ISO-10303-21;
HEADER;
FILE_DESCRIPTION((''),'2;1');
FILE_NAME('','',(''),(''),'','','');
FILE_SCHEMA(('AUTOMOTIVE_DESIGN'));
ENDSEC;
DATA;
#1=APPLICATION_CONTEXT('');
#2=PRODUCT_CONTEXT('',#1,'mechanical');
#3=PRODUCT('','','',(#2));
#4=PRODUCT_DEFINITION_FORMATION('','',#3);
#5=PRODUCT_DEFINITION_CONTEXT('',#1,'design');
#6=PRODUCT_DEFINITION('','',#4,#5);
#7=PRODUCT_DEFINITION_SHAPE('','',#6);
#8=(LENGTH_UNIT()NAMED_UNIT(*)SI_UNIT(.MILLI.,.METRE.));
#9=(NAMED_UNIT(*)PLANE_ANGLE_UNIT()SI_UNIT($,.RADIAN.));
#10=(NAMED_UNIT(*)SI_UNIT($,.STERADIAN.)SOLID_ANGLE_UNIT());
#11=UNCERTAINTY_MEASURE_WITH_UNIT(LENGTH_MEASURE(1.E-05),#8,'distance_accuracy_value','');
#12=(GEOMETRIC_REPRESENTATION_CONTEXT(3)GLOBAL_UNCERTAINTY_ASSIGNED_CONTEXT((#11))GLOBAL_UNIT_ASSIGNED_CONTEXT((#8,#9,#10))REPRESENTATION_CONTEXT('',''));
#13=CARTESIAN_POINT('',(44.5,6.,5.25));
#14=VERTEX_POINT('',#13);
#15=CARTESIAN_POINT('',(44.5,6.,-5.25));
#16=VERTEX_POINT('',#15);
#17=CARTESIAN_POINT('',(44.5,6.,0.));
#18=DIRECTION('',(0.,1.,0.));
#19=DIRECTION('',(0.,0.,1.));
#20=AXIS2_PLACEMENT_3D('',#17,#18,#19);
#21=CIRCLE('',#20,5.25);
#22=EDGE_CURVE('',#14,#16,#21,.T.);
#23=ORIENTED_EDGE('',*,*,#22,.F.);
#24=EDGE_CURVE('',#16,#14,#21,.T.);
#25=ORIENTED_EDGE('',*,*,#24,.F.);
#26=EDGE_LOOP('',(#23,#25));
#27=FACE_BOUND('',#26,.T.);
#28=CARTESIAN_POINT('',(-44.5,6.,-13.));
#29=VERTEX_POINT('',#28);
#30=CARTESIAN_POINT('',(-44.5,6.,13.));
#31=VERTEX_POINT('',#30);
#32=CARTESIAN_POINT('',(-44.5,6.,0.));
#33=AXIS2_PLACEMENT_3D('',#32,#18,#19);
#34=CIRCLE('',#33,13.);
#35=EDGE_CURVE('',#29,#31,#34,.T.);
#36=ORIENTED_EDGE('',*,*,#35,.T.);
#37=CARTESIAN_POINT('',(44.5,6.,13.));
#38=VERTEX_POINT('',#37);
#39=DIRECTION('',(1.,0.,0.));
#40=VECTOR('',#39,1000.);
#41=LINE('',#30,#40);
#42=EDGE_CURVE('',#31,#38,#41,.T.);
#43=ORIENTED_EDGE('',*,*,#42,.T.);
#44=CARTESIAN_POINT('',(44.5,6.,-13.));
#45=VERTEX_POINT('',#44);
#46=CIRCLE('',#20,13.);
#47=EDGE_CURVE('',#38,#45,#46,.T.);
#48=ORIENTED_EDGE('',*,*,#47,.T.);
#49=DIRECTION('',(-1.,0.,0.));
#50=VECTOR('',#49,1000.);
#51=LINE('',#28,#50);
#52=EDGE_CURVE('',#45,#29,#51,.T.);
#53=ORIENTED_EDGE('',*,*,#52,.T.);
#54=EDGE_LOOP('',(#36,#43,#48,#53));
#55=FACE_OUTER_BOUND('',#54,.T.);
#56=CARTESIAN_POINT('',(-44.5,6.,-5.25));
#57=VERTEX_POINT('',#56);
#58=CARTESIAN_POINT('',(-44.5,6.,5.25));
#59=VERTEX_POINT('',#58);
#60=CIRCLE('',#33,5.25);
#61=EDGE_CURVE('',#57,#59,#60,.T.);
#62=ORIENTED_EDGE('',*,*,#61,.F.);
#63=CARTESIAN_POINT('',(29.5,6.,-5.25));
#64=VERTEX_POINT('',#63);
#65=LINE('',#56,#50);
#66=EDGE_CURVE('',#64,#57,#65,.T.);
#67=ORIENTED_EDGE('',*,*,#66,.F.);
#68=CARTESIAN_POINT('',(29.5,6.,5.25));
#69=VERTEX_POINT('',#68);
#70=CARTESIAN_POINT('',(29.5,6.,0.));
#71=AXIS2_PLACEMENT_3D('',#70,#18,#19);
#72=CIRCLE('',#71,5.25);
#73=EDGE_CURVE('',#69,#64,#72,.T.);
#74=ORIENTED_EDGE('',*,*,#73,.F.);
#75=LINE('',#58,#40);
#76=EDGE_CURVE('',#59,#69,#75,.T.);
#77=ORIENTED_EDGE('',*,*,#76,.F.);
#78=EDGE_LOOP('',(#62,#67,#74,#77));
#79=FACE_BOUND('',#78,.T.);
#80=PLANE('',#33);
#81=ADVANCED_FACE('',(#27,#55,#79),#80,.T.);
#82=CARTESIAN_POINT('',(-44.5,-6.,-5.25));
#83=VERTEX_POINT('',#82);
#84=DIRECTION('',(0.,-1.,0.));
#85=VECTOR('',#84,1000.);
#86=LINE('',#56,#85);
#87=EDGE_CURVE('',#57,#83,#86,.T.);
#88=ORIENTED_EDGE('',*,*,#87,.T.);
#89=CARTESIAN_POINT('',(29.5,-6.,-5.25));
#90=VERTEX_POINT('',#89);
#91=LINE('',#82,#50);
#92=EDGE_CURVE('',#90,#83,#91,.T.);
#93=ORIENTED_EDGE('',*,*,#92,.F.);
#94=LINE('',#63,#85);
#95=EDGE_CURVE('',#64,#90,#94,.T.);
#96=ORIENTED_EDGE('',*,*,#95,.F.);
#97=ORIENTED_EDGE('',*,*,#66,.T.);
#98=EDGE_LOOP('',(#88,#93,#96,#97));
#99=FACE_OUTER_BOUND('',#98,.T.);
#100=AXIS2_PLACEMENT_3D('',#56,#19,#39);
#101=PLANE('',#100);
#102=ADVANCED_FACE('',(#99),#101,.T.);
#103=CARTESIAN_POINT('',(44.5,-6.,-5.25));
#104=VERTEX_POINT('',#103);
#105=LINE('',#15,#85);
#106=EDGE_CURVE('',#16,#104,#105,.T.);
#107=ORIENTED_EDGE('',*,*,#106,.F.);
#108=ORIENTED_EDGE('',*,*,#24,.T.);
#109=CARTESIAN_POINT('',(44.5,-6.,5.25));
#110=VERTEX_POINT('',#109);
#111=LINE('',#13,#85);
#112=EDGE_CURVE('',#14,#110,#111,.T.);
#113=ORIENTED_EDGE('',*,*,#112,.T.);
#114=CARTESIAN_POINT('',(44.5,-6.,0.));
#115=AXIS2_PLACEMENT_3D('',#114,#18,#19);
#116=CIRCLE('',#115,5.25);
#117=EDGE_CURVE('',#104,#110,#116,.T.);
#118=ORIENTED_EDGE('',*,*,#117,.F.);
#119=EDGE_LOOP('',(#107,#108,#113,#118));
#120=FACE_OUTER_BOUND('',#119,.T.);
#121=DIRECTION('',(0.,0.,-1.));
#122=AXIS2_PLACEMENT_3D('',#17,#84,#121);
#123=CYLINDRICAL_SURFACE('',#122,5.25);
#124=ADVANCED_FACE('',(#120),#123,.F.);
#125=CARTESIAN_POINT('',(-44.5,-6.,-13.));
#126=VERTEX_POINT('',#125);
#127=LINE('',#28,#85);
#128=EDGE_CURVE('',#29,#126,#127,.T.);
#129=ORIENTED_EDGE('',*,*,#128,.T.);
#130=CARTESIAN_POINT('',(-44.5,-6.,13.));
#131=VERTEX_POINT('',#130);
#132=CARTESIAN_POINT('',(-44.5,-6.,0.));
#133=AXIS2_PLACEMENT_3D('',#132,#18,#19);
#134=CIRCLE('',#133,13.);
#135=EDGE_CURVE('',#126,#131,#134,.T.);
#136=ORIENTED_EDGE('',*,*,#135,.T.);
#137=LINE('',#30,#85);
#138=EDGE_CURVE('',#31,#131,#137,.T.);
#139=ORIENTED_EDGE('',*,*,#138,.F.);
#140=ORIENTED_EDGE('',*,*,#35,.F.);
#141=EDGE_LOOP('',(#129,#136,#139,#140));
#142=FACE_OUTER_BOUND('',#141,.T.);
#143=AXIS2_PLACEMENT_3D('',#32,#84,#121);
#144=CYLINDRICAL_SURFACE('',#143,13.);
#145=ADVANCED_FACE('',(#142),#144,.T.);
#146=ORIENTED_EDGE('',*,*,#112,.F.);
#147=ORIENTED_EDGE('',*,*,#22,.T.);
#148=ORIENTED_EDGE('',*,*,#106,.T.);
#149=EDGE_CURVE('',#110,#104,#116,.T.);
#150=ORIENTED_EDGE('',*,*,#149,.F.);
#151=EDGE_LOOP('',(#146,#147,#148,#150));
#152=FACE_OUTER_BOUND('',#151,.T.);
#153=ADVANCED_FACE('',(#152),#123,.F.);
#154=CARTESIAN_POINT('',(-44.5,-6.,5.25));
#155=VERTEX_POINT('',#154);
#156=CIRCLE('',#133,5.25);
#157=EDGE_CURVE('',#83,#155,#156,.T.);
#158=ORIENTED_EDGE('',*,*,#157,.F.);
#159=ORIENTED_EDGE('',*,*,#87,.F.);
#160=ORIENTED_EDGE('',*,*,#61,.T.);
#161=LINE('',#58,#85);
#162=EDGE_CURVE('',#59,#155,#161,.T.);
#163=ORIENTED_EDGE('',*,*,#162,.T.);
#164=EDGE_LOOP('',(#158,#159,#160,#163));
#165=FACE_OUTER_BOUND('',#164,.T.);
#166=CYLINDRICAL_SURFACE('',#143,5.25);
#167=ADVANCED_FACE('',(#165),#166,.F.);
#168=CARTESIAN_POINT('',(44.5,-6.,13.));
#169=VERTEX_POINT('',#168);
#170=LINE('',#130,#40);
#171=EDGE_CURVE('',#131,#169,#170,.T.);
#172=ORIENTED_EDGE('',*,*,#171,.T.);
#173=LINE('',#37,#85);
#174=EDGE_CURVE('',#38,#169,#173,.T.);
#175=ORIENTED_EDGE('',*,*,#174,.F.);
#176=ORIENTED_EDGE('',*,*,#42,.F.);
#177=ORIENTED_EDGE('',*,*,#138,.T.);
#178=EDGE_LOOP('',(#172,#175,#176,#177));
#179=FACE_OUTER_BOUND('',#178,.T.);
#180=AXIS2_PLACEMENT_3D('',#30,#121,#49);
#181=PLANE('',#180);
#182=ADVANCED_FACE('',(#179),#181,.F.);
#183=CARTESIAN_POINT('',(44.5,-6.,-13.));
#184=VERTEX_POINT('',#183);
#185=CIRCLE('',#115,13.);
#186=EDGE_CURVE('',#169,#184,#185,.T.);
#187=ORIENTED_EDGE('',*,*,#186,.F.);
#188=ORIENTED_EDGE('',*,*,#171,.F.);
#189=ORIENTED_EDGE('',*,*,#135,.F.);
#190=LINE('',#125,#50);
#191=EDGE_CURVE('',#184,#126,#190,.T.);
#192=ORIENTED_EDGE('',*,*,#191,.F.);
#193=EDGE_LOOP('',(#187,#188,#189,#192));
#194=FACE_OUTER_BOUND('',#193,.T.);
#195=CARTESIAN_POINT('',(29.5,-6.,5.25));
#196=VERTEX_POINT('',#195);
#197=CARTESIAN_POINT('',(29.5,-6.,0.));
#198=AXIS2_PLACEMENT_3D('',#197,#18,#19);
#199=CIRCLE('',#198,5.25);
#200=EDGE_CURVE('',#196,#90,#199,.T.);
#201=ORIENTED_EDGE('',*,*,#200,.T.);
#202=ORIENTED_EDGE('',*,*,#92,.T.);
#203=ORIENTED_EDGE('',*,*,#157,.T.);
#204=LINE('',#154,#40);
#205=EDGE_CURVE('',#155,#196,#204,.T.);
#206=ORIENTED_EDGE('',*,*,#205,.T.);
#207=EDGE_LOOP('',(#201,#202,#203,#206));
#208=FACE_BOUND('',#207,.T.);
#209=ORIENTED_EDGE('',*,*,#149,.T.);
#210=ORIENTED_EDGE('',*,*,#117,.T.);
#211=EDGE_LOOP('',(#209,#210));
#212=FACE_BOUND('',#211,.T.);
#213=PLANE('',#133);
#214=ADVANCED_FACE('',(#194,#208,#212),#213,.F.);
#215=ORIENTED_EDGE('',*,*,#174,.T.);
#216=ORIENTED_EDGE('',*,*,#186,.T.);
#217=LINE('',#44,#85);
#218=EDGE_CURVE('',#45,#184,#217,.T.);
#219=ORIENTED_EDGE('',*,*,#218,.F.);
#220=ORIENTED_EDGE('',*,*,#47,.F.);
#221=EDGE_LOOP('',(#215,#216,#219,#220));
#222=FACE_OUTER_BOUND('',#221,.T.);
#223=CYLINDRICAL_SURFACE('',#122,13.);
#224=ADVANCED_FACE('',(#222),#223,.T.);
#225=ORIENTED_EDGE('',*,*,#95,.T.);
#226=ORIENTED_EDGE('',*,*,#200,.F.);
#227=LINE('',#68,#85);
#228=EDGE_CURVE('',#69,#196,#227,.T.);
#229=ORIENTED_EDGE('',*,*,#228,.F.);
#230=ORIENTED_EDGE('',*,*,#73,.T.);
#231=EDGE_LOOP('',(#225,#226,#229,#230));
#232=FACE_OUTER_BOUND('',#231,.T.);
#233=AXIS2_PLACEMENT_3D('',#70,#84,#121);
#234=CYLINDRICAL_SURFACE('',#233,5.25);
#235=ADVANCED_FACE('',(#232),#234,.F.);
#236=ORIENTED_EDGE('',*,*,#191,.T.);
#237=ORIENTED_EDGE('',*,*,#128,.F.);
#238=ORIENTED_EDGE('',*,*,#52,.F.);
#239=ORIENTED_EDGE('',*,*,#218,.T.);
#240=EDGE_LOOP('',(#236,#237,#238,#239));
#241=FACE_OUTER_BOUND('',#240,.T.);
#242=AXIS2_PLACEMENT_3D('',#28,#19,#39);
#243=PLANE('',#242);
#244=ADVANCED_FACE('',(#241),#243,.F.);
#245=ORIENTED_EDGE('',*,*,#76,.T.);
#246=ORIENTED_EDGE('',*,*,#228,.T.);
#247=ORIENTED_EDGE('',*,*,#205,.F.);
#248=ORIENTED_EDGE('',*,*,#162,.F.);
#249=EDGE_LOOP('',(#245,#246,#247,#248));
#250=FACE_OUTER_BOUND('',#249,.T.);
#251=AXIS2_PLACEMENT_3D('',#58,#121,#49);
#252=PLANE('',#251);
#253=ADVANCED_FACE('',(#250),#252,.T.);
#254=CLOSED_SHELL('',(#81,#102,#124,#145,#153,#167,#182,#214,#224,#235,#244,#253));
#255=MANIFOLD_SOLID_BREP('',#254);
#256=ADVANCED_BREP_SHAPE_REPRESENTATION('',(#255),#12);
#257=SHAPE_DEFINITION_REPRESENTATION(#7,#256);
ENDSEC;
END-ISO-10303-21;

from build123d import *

# Parameters (mm, degrees)
SKETCH1_R           = 5.25
BOSS_EXTRUDE1_DEPTH = 6


with BuildPart() as part:
    # Sketch1 → Boss-Extrude1 (new, symmetric)
    with BuildSketch(Plane(origin=(0, 0, 0), x_dir=(1, 0, 0), z_dir=(0, 1, 0))):
        with BuildLine():
            Line((-44.5, 13), (44.5, 13))
            ThreePointArc((44.5, 13), (57.5, 0), (44.5, -13))
            Line((44.5, -13), (-44.5, -13))
            ThreePointArc((-44.5, -13), (-57.5, 0), (-44.5, 13))
        make_face()
        with Locations(Location((44.5, 0, 0), (0, 0, 270))):
            Circle(SKETCH1_R, mode=Mode.SUBTRACT)
        with BuildLine():
            Line((-44.5, 5.25), (29.5, 5.25))
            ThreePointArc((29.5, 5.25), (34.75, 0), (29.5, -5.25))
            Line((29.5, -5.25), (-44.5, -5.25))
            ThreePointArc((-44.5, -5.25), (-49.75, 0), (-44.5, 5.25))
        make_face(mode=Mode.SUBTRACT)
    extrude(amount=BOSS_EXTRUDE1_DEPTH, both=True)


solid = part.part
